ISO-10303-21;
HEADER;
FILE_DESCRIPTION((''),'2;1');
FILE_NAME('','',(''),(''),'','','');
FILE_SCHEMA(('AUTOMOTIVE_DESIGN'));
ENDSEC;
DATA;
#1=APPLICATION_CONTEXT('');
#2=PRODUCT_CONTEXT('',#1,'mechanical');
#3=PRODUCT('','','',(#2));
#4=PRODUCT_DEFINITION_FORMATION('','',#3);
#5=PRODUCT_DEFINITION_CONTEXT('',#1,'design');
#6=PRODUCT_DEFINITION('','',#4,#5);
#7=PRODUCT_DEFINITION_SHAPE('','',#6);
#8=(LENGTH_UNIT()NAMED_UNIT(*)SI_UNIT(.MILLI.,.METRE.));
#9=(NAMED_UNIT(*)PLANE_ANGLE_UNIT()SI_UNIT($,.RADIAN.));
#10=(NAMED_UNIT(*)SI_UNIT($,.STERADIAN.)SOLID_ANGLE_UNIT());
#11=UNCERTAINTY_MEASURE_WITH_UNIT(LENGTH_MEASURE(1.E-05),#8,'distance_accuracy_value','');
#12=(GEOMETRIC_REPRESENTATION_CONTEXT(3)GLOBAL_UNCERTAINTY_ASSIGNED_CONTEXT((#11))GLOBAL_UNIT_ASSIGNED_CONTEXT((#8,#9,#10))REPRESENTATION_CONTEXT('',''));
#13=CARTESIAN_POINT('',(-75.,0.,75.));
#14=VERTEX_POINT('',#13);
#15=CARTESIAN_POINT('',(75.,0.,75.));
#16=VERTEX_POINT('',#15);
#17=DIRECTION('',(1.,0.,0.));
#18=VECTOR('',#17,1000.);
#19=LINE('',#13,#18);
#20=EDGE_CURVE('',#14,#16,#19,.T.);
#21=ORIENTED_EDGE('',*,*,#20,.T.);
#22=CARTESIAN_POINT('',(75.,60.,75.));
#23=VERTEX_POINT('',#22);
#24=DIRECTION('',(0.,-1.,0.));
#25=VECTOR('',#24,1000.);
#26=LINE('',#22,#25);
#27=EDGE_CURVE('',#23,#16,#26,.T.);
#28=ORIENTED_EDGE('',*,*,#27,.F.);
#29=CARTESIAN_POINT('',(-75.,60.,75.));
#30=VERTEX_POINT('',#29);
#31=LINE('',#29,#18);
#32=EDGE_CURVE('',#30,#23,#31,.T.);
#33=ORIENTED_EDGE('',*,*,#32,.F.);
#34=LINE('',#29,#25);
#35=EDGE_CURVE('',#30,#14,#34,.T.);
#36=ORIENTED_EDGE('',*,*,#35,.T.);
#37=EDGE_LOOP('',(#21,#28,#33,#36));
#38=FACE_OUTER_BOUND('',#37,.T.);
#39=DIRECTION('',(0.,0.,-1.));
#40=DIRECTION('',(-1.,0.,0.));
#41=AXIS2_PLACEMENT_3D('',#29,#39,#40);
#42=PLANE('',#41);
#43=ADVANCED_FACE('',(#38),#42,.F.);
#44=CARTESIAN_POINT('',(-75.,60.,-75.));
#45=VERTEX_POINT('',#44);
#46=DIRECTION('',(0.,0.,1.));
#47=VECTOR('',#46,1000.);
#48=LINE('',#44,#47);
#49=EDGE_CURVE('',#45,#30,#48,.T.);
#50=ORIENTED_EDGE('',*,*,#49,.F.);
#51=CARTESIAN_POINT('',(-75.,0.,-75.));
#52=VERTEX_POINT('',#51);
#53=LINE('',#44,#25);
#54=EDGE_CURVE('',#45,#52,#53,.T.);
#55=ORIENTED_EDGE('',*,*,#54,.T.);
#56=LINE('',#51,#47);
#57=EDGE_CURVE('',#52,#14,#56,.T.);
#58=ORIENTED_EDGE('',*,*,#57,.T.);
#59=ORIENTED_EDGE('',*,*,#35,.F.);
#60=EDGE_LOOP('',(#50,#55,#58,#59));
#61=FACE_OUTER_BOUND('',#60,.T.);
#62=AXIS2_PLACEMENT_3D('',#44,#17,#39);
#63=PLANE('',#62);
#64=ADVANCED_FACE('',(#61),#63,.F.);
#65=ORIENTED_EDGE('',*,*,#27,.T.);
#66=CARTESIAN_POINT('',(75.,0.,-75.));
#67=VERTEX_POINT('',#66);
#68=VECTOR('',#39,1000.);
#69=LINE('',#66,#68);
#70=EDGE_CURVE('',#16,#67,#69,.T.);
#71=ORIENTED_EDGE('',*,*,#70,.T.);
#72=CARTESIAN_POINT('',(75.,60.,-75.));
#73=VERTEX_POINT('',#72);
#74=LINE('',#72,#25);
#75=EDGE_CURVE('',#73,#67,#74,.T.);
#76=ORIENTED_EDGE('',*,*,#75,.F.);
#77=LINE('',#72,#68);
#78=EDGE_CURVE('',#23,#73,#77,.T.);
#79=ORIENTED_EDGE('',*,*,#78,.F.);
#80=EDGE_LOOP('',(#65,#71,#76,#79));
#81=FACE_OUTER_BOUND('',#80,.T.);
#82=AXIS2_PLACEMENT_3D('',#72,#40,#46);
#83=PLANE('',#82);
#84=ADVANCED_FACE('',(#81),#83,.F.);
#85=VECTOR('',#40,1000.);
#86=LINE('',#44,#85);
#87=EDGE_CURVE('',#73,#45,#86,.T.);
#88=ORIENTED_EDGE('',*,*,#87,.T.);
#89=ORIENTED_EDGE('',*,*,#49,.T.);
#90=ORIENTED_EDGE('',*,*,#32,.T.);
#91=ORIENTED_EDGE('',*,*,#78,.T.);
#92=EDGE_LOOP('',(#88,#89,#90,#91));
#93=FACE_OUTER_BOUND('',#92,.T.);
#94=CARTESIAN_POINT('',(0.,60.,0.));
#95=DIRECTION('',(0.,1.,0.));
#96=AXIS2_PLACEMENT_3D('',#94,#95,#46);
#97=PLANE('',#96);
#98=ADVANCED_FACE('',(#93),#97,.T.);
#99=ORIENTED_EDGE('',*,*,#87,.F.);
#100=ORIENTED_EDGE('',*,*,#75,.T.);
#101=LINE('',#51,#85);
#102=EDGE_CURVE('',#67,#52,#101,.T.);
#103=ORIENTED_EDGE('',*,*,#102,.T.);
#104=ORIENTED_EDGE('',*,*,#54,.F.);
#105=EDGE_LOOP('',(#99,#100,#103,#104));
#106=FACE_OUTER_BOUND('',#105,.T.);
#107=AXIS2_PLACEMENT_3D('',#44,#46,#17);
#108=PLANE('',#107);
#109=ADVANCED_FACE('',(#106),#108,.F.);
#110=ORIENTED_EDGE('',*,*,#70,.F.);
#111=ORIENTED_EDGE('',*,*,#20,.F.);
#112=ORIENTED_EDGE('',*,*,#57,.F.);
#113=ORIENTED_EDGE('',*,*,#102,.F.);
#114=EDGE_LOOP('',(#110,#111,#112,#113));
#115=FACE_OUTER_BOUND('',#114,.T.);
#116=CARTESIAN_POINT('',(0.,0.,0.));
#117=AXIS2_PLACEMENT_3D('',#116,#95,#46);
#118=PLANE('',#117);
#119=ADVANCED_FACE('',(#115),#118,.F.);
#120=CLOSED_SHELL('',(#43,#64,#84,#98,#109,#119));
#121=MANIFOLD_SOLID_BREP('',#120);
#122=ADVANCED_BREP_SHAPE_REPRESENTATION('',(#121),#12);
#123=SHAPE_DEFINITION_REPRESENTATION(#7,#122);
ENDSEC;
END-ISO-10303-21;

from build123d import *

# Parameters (mm, degrees)
SKETCH1_W           = 150
SKETCH1_H           = 150
BOSS_EXTRUDE1_DEPTH = 60


with BuildPart() as part:
    # Sketch1 → Boss-Extrude1 (new body)
    with BuildSketch(Plane(origin=(0, 0, 0), x_dir=(1, 0, 0), z_dir=(0, 1, 0))):
        Rectangle(SKETCH1_W, SKETCH1_H)
    extrude(amount=BOSS_EXTRUDE1_DEPTH)


solid = part.part
